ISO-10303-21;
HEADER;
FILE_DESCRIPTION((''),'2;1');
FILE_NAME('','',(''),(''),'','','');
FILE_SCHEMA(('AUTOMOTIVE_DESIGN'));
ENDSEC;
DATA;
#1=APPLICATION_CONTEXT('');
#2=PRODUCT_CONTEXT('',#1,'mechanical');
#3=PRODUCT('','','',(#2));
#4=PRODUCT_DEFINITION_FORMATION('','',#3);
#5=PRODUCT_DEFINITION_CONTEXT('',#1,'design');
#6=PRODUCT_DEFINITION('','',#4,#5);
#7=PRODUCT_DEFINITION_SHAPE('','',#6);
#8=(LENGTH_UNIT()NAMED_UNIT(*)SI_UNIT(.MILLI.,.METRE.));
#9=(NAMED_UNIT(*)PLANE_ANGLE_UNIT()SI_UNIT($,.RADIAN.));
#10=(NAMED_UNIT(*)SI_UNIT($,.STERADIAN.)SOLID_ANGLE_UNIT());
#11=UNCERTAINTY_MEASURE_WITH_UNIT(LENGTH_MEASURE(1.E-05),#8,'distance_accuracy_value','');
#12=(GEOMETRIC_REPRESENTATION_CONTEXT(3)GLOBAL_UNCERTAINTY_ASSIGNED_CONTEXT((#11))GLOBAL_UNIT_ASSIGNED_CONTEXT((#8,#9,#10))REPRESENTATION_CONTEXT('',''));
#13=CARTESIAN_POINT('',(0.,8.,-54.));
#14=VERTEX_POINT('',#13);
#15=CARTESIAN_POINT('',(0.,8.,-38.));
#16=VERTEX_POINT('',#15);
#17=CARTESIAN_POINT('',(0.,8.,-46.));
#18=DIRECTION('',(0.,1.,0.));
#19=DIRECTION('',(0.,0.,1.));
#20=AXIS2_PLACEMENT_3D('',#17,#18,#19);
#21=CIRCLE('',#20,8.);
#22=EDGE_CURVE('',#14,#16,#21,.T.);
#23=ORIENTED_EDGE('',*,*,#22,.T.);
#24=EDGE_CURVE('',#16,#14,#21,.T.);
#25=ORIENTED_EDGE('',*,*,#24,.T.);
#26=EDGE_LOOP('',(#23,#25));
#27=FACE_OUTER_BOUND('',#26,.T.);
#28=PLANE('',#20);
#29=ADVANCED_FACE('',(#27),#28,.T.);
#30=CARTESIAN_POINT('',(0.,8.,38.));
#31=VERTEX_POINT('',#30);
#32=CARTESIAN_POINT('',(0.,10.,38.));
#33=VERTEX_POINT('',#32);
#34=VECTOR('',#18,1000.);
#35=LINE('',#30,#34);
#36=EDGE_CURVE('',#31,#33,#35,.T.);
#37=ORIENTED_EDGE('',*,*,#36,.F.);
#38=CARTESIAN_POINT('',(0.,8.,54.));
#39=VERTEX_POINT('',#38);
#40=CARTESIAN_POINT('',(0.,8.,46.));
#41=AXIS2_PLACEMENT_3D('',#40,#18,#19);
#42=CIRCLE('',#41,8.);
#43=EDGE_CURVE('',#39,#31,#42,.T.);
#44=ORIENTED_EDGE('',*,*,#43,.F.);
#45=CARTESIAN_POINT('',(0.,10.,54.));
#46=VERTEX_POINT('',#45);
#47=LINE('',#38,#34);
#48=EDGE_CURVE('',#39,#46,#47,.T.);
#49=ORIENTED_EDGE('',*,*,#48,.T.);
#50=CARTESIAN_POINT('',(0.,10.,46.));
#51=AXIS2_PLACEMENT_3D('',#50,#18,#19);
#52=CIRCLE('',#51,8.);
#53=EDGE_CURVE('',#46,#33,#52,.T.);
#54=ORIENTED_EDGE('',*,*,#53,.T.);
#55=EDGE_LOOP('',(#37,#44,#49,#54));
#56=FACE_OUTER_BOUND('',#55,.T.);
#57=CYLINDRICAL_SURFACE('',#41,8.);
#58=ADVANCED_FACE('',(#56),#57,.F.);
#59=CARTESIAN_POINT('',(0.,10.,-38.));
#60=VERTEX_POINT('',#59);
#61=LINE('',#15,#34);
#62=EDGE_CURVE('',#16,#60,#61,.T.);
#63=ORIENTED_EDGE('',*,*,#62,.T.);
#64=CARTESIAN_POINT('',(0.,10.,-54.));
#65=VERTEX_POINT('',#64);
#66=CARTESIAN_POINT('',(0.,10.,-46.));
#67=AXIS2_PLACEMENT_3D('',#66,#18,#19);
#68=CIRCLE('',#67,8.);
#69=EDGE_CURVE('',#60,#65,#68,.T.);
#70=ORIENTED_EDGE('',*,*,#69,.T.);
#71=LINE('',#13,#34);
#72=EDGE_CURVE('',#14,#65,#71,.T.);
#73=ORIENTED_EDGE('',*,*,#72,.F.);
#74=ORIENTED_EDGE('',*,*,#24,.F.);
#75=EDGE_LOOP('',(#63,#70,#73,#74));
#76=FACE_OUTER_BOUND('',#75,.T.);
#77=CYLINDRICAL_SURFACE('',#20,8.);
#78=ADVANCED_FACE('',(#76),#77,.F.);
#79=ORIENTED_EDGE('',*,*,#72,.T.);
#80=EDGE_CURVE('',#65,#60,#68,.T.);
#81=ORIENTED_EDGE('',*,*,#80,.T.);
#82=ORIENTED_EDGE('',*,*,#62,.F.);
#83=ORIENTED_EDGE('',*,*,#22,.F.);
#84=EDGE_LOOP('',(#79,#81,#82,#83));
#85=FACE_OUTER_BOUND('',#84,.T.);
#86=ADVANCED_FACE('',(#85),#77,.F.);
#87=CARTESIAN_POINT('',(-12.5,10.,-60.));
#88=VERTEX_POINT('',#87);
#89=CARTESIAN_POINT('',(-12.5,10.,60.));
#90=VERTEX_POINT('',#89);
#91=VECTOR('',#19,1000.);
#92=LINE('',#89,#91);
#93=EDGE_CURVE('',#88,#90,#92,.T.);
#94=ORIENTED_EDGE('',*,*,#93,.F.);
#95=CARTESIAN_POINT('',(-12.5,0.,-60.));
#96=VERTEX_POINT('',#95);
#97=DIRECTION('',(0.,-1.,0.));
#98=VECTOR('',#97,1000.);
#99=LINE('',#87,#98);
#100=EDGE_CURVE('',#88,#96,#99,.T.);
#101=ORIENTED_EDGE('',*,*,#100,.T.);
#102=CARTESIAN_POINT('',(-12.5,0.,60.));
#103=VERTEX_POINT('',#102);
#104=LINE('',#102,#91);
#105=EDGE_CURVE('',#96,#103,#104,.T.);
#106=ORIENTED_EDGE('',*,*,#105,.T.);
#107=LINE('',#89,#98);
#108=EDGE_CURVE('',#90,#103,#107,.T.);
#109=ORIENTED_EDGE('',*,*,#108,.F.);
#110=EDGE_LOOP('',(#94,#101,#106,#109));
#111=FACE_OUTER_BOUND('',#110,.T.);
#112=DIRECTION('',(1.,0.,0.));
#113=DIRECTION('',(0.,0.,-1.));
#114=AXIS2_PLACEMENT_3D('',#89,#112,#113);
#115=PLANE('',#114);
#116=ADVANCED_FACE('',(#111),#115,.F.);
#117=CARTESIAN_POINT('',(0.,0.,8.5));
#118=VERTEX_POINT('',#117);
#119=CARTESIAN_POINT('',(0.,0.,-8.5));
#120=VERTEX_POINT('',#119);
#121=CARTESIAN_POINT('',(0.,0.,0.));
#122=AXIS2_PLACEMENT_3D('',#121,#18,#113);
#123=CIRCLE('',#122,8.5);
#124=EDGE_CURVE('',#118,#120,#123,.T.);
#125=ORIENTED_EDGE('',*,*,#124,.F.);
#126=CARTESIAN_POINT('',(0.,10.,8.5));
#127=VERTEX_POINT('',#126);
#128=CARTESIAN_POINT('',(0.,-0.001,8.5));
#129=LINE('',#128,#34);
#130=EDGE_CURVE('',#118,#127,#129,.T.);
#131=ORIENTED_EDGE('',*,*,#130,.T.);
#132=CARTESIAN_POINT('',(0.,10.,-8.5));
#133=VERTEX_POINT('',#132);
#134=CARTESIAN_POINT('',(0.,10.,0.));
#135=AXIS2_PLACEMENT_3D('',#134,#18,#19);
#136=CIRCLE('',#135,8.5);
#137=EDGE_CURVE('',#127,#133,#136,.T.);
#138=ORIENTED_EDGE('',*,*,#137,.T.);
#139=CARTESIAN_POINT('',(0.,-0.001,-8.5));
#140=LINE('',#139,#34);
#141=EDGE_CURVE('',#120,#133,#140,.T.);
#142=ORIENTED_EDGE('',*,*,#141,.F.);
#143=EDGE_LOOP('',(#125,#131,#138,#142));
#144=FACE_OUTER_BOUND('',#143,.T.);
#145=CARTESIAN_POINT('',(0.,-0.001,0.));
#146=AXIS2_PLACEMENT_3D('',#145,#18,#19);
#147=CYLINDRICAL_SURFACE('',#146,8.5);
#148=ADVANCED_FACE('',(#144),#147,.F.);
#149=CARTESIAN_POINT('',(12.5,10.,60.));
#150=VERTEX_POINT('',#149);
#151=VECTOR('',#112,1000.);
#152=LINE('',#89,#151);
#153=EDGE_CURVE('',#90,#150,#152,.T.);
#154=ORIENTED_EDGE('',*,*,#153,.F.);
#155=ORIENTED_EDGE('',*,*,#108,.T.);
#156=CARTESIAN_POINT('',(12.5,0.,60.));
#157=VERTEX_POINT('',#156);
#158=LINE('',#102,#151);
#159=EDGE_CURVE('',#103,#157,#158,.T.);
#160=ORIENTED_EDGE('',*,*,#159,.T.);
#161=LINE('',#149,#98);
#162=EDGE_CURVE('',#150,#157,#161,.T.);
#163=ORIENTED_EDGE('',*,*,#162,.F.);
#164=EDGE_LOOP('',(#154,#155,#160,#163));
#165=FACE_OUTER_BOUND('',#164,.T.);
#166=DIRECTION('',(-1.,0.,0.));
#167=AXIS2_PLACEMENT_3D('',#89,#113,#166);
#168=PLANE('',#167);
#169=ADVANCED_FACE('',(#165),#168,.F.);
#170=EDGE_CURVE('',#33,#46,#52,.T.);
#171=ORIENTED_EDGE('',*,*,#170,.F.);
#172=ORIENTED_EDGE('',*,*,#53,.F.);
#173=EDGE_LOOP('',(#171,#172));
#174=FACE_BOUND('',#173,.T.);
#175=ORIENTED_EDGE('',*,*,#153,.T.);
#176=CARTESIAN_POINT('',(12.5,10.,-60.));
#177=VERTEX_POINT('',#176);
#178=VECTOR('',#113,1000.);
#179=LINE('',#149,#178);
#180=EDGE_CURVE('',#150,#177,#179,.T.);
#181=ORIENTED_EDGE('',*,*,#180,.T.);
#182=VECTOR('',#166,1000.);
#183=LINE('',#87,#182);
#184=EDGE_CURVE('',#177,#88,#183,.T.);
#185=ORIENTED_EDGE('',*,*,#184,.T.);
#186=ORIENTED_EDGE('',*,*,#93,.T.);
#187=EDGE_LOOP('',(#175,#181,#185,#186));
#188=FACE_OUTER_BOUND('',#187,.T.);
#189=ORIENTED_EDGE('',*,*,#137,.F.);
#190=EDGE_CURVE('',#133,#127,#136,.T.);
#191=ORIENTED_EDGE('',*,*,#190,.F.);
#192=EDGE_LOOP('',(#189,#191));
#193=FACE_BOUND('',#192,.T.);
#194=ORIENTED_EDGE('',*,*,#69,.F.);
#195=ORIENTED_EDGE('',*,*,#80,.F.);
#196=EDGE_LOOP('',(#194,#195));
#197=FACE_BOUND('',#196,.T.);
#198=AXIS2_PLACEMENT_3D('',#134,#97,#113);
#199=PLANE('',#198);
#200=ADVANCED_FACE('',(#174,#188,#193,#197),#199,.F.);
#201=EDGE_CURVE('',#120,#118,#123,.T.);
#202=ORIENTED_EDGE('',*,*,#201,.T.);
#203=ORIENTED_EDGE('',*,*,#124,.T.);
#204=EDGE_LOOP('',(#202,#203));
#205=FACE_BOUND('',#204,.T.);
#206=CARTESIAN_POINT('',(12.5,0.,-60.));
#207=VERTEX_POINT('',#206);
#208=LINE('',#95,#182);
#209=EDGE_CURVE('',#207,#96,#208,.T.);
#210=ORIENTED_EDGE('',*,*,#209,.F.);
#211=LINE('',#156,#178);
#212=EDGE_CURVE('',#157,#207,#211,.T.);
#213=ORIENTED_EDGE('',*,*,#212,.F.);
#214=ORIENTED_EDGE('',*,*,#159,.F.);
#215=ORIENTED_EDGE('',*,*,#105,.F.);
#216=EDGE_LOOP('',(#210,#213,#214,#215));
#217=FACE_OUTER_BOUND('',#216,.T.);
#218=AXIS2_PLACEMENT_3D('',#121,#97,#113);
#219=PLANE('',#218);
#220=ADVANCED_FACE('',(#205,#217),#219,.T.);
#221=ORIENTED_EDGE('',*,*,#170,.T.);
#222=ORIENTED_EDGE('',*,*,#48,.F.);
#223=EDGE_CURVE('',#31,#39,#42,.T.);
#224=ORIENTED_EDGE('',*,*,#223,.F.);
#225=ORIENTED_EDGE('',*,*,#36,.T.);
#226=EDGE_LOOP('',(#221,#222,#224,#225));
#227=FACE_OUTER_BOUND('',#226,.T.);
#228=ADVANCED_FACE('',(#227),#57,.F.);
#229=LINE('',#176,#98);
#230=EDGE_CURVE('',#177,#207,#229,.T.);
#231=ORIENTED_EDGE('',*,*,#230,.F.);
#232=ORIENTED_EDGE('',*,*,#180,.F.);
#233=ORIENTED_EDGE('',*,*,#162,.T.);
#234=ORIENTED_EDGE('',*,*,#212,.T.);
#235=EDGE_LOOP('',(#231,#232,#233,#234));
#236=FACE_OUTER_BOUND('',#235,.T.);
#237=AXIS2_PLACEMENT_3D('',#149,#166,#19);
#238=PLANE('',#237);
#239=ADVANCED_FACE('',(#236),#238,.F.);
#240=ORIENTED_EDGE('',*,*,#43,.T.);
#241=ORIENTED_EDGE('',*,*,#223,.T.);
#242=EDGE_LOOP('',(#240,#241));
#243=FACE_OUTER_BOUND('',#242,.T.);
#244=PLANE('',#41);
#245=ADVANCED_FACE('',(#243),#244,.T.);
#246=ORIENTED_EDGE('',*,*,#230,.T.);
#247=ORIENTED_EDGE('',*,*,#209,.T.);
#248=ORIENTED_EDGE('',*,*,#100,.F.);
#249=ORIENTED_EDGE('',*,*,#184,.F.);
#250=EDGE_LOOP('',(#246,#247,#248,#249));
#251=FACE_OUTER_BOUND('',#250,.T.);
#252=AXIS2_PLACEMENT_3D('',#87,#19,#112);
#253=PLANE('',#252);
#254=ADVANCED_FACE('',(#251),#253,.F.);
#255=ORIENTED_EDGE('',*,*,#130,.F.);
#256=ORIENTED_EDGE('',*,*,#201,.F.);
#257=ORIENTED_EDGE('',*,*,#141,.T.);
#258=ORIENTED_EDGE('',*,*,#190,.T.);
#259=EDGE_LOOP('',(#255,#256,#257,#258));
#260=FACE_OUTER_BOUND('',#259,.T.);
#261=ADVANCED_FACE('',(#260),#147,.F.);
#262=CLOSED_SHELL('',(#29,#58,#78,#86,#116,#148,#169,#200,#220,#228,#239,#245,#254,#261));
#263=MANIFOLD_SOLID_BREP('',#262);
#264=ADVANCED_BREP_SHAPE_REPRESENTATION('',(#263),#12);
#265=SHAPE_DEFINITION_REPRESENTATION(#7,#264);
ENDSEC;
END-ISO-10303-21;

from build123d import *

# Parameters (mm, degrees)
SKETCH_1_W          = 25
SKETCH_1_H          = 120
EXTRUDE_1_DEPTH     = 10
SKETCH_2_R          = 8
CUT_EXTRUDE_1_DEPTH = 2
CUT_EXTRUDE_2_REACH = 64.099
SKETCH_3_R          = 8.5


with BuildPart() as part:
    # 草图1 → 凸台-拉伸1 (new body)
    with BuildSketch(Plane(origin=(0, 0, 0), x_dir=(1, 0, 0), z_dir=(0, 1, 0))):
        Rectangle(SKETCH_1_W, SKETCH_1_H)
    extrude(amount=EXTRUDE_1_DEPTH)

    # 草图2 → 切除-拉伸1 (cut)
    with BuildSketch(Plane(origin=(0, 10, 0), x_dir=(1, 0, 0), z_dir=(0, 1, 0))):
        with Locations(Location((0, 46, 0), (0, 0, 270))):
            Circle(SKETCH_2_R)
        with Locations(Location((0, -46, 0), (0, 0, 270))):
            Circle(SKETCH_2_R)
    extrude(amount=-CUT_EXTRUDE_1_DEPTH, mode=Mode.SUBTRACT)

    # 草图3 → 切除-拉伸2 (cut, up to next)
    with BuildSketch(Plane(origin=(0, 10, 0), x_dir=(1, 0, 0), z_dir=(0, 1, 0)), mode=Mode.PRIVATE) as cut_extrude_2_sk1:
        with Locations(Location((0, 0, 0), (0, 0, 270))):
            Circle(SKETCH_3_R)
    cut_extrude_2_tool1 = extrude(cut_extrude_2_sk1.sketch, amount=-CUT_EXTRUDE_2_REACH, mode=Mode.PRIVATE) & part.part
    add(cut_extrude_2_tool1.solids().sort_by_distance((0, 10, 0))[0], mode=Mode.SUBTRACT)


solid = part.part
